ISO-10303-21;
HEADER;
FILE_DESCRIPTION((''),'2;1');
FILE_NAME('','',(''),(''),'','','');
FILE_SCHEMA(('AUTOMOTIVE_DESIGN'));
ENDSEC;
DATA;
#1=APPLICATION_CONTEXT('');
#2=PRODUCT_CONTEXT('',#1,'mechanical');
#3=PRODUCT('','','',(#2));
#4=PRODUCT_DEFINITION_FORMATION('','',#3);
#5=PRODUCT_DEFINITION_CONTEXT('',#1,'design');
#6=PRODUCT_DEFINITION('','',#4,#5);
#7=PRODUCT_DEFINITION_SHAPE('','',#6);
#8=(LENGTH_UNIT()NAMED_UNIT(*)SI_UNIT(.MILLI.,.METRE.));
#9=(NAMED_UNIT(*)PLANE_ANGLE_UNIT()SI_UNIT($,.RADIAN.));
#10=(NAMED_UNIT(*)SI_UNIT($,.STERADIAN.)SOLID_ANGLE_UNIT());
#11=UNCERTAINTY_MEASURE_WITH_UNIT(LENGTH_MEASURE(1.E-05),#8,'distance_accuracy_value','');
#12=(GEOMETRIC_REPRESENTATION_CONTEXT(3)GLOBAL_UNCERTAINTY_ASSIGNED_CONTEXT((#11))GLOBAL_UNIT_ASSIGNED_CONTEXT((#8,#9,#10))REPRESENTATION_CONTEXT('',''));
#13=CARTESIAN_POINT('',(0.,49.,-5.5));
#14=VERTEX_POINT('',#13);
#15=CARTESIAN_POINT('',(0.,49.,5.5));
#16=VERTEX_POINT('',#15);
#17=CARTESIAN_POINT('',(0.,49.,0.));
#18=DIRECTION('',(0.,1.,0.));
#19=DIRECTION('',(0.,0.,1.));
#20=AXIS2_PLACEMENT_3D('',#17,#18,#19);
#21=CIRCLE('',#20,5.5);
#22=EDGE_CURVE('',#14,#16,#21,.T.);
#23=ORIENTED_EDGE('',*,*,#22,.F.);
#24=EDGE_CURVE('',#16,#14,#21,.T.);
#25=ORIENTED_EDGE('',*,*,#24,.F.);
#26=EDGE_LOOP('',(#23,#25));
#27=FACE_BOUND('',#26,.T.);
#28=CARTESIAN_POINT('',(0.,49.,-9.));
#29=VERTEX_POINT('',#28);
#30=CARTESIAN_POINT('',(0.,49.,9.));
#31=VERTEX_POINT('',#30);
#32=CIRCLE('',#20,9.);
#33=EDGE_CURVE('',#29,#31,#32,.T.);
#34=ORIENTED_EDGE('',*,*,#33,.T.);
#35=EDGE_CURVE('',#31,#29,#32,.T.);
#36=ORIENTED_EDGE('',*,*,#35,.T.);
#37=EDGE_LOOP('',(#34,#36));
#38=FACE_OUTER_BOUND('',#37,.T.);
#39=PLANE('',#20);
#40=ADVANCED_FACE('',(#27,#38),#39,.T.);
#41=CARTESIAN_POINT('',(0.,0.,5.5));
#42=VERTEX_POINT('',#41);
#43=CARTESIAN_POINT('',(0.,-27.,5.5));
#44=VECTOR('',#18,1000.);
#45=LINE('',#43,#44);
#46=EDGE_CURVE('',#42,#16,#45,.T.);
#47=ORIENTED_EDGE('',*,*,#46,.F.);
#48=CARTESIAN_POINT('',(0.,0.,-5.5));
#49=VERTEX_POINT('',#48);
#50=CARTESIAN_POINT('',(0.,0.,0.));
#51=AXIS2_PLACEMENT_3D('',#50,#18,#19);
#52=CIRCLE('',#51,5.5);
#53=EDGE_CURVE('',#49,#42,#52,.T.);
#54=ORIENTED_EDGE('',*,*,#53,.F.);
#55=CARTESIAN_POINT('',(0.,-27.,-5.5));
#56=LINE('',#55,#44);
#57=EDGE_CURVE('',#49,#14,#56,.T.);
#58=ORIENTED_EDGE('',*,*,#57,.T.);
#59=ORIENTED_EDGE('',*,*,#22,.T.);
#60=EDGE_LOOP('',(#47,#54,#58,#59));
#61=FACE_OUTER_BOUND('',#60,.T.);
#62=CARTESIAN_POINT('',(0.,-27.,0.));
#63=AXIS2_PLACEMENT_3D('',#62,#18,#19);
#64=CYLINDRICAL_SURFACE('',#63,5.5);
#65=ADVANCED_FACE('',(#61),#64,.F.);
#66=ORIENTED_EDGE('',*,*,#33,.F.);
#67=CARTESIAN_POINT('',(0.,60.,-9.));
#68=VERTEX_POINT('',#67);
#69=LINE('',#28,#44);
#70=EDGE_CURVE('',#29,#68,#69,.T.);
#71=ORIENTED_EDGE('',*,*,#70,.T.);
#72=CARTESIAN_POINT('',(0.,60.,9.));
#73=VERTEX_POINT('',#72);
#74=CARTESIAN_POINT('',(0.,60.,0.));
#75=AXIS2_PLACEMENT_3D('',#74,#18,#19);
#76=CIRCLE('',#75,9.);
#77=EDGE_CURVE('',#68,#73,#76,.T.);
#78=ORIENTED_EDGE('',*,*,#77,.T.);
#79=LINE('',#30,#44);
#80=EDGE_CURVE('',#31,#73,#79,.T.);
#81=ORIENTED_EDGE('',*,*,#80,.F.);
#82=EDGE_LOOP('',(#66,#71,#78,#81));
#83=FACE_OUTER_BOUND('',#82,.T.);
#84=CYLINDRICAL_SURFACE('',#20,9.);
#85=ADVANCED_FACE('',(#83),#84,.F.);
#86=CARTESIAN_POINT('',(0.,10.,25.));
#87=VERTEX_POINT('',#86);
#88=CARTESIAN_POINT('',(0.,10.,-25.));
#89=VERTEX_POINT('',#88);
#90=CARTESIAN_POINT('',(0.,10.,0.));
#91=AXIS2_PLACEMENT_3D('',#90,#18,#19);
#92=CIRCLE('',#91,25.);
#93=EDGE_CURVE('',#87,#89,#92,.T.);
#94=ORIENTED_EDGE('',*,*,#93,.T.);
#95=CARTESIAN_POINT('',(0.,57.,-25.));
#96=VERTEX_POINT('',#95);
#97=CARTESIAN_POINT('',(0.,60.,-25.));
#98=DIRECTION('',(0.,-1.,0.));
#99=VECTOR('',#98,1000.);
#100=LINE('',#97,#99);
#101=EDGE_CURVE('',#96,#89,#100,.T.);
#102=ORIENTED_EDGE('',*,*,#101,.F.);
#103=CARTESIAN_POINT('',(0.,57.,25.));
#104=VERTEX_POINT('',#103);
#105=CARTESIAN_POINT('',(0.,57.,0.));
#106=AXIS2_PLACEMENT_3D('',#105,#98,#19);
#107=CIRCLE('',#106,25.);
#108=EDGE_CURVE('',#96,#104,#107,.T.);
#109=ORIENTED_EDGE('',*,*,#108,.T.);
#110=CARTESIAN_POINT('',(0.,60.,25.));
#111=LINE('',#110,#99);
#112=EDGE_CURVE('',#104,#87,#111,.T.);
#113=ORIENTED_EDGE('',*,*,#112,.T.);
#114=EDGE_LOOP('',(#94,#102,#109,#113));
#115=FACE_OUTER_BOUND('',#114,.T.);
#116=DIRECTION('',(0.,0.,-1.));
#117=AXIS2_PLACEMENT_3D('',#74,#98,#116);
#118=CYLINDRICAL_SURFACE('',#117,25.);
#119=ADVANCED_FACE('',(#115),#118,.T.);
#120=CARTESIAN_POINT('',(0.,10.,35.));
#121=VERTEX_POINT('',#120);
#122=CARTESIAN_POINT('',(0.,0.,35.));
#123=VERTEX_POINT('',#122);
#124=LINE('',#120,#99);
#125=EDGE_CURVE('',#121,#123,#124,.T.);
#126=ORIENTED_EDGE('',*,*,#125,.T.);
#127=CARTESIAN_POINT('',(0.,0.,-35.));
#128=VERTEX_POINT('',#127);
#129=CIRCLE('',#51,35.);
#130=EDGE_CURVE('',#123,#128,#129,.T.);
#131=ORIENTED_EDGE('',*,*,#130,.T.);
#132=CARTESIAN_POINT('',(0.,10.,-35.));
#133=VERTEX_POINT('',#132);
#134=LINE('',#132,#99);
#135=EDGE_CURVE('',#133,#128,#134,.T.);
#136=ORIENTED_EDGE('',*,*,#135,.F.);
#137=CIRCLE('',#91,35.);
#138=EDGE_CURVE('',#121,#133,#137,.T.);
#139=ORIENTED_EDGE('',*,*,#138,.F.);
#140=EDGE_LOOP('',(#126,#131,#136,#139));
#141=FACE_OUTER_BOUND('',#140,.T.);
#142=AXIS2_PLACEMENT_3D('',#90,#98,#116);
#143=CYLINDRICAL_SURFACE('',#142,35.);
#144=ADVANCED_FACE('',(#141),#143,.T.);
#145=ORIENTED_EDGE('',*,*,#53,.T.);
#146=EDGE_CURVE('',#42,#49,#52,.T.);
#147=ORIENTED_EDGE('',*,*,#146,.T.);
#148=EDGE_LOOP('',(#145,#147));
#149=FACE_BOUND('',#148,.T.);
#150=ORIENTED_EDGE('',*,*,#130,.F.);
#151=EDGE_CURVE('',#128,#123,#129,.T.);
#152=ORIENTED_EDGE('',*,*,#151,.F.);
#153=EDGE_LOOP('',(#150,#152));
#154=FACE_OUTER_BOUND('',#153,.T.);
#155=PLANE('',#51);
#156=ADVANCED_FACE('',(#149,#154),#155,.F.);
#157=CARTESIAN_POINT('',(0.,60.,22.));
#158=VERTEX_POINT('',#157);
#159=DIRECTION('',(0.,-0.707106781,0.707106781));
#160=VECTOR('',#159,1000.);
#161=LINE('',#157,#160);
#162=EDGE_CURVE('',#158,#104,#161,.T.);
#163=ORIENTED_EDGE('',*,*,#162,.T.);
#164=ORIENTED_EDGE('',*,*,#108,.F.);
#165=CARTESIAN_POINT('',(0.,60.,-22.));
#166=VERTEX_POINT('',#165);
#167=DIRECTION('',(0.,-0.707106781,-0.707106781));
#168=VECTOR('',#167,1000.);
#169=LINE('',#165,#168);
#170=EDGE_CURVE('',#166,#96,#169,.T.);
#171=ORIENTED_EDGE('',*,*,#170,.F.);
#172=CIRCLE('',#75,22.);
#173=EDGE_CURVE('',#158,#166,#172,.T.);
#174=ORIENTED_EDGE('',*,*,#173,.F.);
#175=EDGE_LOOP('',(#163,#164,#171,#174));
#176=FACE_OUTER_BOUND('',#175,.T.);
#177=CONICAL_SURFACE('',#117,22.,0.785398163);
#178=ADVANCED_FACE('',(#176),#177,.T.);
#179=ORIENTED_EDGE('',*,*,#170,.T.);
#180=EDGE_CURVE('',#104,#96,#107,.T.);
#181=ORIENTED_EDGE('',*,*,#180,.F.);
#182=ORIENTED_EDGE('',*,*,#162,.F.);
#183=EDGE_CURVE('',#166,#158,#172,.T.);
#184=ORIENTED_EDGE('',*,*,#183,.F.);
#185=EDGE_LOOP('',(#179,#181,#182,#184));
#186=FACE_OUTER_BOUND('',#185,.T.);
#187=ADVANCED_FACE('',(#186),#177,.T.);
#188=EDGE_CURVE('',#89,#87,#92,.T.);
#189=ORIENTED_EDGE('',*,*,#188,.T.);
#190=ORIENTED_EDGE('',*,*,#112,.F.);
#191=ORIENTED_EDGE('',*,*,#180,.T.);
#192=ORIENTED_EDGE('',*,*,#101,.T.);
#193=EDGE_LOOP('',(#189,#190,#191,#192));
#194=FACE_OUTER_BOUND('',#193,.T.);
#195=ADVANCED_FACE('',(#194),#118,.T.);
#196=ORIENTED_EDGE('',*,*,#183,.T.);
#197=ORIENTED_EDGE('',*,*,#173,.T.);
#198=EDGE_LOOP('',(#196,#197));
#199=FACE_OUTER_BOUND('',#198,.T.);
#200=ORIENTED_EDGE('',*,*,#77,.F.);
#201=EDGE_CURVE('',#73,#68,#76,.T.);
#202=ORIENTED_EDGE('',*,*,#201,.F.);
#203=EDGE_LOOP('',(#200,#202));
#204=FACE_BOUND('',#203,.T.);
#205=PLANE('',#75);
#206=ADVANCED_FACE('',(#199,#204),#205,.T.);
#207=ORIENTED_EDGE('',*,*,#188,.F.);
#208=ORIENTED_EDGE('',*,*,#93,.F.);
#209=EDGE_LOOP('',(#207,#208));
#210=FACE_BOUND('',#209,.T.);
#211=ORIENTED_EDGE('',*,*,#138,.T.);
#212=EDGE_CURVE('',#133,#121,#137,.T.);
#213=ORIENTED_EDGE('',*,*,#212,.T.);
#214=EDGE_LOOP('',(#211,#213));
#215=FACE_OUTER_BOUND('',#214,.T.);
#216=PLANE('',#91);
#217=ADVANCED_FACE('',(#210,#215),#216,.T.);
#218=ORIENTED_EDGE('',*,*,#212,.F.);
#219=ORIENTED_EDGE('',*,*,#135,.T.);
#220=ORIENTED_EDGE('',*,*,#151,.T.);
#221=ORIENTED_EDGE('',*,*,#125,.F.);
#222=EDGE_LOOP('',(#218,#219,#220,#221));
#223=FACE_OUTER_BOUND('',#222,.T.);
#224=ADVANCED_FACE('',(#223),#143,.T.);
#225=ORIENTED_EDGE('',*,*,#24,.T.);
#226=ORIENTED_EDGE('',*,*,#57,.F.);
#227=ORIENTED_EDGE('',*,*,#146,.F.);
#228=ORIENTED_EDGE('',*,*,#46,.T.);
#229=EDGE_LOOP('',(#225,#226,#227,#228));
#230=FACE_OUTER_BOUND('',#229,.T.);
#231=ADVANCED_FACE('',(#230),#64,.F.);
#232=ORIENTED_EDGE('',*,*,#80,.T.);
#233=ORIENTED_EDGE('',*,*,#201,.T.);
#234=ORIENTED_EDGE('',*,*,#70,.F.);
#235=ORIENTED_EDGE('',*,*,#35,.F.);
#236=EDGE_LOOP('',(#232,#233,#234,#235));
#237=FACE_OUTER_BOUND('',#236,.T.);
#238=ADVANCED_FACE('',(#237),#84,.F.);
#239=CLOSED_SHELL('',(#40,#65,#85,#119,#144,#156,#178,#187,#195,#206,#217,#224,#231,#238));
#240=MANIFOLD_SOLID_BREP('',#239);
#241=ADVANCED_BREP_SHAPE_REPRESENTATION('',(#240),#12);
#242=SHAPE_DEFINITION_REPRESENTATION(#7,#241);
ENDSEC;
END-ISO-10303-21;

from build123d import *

# Parameters (mm, degrees)
SKETCH1_R           = 35
BOSS_EXTRUDE1_DEPTH = 10
SKETCH2_R           = 25
BOSS_EXTRUDE2_DEPTH = 50
CHAMFER1_SIZE       = 3
SKETCH3_R           = 9
CUT_EXTRUDE1_DEPTH  = 11
SKETCH4_R           = 5.5
CUT_EXTRUDE2_DEPTH  = 76


with BuildPart() as part:
    # Sketch1 → Boss-Extrude1 (new body)
    with BuildSketch(Plane(origin=(0, 0, 0), x_dir=(1, 0, 0), z_dir=(0, 1, 0))):
        with Locations(Location((0, 0, 0), (0, 0, 270))):
            Circle(SKETCH1_R)
    extrude(amount=BOSS_EXTRUDE1_DEPTH)

    # Sketch2 → Boss-Extrude2 (add)
    with BuildSketch(Plane(origin=(0, 10, 0), x_dir=(1, 0, 0), z_dir=(0, 1, 0))):
        with Locations(Location((0, 0, 0), (0, 0, 270))):
            Circle(SKETCH2_R)
    extrude(amount=BOSS_EXTRUDE2_DEPTH)

    # Chamfer1
    chamfer1_edges = [part.edges().sort_by_distance(p)[0] for p in [
        (0, 60, -25),
    ]]
    chamfer(chamfer1_edges, length=CHAMFER1_SIZE)

    # Sketch3 → Cut-Extrude1 (cut)
    with BuildSketch(Plane(origin=(0, 60, 0), x_dir=(1, 0, 0), z_dir=(0, 1, 0))):
        with Locations(Location((0, 0, 0), (0, 0, 270))):
            Circle(SKETCH3_R)
    extrude(amount=-CUT_EXTRUDE1_DEPTH, mode=Mode.SUBTRACT)

    # Sketch4 → Cut-Extrude2 (cut)
    with BuildSketch(Plane(origin=(0, 49, 0), x_dir=(1, 0, 0), z_dir=(0, 1, 0))):
        with Locations(Location((0, 0, 0), (0, 0, 270))):
            Circle(SKETCH4_R)
    extrude(amount=-CUT_EXTRUDE2_DEPTH, mode=Mode.SUBTRACT)


solid = part.part
